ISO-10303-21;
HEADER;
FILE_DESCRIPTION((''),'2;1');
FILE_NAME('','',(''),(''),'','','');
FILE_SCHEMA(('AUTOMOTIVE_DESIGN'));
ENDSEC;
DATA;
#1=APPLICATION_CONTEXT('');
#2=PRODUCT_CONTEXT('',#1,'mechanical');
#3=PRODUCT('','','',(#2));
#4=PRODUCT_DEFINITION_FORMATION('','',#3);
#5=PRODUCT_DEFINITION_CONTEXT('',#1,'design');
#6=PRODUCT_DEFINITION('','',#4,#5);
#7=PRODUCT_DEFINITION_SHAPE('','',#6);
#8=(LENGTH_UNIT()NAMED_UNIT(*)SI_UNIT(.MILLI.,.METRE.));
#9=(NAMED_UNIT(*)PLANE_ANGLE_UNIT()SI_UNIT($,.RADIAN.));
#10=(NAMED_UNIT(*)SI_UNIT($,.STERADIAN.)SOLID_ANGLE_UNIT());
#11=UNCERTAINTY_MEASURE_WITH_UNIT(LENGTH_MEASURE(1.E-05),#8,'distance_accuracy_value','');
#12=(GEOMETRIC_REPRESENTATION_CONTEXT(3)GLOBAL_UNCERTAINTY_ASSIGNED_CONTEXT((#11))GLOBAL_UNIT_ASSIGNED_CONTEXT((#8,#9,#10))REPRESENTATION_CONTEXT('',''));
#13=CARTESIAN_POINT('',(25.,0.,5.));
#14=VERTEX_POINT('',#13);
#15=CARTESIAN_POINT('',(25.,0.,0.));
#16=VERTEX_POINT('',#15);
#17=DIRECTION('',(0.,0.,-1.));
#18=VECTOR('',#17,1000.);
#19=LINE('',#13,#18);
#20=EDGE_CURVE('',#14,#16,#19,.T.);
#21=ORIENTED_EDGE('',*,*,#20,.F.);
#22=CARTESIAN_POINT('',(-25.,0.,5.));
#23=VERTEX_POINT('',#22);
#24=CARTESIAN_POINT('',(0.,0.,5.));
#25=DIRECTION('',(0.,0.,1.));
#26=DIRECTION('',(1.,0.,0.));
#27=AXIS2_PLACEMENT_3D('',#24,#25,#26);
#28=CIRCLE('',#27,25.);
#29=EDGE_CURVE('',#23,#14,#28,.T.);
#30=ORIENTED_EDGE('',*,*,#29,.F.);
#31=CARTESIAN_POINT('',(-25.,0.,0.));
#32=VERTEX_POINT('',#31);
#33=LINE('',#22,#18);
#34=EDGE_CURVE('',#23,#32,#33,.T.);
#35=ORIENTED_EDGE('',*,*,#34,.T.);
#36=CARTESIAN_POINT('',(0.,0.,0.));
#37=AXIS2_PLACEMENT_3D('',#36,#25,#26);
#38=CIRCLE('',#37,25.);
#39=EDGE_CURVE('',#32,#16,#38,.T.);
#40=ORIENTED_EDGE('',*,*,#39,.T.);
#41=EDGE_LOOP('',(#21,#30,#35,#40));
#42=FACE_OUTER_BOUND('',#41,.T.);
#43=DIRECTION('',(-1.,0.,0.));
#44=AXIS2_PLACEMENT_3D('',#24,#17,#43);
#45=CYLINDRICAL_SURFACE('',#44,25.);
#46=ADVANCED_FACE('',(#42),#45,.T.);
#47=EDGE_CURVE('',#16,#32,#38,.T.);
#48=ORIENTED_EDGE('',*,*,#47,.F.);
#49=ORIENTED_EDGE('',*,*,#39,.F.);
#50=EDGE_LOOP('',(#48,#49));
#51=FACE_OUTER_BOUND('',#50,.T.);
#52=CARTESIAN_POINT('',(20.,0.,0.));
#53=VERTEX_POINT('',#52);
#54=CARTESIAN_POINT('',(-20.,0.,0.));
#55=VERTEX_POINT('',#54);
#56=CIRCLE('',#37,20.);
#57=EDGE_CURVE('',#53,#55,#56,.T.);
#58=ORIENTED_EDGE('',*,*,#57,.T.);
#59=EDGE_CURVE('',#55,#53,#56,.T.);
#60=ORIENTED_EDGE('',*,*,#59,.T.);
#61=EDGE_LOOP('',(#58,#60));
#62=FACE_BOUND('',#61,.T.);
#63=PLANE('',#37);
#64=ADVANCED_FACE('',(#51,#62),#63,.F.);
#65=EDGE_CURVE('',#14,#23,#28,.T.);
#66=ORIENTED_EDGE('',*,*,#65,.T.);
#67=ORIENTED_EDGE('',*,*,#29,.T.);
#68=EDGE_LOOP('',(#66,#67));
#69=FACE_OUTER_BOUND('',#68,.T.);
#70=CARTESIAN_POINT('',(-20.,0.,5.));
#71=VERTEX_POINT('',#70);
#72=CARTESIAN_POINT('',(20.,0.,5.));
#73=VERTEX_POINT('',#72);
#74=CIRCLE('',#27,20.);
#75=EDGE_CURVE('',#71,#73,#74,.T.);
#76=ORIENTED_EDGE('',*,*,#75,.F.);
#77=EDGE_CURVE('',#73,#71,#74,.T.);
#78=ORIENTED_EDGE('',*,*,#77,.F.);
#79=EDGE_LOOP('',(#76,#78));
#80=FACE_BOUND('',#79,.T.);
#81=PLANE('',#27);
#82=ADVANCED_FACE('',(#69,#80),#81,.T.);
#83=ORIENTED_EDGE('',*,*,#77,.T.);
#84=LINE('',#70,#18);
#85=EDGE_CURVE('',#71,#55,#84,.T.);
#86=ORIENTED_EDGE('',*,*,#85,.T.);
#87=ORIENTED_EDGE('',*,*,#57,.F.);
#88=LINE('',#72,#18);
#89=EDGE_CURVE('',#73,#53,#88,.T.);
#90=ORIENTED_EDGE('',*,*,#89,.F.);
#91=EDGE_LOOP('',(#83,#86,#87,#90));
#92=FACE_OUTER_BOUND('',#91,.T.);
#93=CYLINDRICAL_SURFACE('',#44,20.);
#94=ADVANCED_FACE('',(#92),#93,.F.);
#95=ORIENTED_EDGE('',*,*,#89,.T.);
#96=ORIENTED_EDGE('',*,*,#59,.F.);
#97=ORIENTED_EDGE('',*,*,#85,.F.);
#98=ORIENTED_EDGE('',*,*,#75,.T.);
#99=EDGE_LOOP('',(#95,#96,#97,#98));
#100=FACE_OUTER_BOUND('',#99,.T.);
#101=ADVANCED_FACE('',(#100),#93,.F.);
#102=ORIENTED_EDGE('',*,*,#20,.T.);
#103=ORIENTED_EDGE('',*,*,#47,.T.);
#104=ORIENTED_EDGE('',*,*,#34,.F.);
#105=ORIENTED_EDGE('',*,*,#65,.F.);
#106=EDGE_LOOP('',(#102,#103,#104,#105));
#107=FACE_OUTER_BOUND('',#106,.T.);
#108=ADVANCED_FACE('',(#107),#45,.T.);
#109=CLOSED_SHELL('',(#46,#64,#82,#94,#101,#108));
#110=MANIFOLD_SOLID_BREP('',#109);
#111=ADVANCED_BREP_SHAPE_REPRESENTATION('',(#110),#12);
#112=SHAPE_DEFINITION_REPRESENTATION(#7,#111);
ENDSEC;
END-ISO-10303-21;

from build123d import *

# Parameters (mm, degrees)
SKETCH_1_R      = 25
SKETCH_1_R_2    = 20
EXTRUDE_1_DEPTH = 5


with BuildPart() as part:
    # 草图1 → 凸台-拉伸1 (new body)
    with BuildSketch(Plane.XY):
        Circle(SKETCH_1_R)
        Circle(SKETCH_1_R_2, mode=Mode.SUBTRACT)
    extrude(amount=EXTRUDE_1_DEPTH)


solid = part.part
